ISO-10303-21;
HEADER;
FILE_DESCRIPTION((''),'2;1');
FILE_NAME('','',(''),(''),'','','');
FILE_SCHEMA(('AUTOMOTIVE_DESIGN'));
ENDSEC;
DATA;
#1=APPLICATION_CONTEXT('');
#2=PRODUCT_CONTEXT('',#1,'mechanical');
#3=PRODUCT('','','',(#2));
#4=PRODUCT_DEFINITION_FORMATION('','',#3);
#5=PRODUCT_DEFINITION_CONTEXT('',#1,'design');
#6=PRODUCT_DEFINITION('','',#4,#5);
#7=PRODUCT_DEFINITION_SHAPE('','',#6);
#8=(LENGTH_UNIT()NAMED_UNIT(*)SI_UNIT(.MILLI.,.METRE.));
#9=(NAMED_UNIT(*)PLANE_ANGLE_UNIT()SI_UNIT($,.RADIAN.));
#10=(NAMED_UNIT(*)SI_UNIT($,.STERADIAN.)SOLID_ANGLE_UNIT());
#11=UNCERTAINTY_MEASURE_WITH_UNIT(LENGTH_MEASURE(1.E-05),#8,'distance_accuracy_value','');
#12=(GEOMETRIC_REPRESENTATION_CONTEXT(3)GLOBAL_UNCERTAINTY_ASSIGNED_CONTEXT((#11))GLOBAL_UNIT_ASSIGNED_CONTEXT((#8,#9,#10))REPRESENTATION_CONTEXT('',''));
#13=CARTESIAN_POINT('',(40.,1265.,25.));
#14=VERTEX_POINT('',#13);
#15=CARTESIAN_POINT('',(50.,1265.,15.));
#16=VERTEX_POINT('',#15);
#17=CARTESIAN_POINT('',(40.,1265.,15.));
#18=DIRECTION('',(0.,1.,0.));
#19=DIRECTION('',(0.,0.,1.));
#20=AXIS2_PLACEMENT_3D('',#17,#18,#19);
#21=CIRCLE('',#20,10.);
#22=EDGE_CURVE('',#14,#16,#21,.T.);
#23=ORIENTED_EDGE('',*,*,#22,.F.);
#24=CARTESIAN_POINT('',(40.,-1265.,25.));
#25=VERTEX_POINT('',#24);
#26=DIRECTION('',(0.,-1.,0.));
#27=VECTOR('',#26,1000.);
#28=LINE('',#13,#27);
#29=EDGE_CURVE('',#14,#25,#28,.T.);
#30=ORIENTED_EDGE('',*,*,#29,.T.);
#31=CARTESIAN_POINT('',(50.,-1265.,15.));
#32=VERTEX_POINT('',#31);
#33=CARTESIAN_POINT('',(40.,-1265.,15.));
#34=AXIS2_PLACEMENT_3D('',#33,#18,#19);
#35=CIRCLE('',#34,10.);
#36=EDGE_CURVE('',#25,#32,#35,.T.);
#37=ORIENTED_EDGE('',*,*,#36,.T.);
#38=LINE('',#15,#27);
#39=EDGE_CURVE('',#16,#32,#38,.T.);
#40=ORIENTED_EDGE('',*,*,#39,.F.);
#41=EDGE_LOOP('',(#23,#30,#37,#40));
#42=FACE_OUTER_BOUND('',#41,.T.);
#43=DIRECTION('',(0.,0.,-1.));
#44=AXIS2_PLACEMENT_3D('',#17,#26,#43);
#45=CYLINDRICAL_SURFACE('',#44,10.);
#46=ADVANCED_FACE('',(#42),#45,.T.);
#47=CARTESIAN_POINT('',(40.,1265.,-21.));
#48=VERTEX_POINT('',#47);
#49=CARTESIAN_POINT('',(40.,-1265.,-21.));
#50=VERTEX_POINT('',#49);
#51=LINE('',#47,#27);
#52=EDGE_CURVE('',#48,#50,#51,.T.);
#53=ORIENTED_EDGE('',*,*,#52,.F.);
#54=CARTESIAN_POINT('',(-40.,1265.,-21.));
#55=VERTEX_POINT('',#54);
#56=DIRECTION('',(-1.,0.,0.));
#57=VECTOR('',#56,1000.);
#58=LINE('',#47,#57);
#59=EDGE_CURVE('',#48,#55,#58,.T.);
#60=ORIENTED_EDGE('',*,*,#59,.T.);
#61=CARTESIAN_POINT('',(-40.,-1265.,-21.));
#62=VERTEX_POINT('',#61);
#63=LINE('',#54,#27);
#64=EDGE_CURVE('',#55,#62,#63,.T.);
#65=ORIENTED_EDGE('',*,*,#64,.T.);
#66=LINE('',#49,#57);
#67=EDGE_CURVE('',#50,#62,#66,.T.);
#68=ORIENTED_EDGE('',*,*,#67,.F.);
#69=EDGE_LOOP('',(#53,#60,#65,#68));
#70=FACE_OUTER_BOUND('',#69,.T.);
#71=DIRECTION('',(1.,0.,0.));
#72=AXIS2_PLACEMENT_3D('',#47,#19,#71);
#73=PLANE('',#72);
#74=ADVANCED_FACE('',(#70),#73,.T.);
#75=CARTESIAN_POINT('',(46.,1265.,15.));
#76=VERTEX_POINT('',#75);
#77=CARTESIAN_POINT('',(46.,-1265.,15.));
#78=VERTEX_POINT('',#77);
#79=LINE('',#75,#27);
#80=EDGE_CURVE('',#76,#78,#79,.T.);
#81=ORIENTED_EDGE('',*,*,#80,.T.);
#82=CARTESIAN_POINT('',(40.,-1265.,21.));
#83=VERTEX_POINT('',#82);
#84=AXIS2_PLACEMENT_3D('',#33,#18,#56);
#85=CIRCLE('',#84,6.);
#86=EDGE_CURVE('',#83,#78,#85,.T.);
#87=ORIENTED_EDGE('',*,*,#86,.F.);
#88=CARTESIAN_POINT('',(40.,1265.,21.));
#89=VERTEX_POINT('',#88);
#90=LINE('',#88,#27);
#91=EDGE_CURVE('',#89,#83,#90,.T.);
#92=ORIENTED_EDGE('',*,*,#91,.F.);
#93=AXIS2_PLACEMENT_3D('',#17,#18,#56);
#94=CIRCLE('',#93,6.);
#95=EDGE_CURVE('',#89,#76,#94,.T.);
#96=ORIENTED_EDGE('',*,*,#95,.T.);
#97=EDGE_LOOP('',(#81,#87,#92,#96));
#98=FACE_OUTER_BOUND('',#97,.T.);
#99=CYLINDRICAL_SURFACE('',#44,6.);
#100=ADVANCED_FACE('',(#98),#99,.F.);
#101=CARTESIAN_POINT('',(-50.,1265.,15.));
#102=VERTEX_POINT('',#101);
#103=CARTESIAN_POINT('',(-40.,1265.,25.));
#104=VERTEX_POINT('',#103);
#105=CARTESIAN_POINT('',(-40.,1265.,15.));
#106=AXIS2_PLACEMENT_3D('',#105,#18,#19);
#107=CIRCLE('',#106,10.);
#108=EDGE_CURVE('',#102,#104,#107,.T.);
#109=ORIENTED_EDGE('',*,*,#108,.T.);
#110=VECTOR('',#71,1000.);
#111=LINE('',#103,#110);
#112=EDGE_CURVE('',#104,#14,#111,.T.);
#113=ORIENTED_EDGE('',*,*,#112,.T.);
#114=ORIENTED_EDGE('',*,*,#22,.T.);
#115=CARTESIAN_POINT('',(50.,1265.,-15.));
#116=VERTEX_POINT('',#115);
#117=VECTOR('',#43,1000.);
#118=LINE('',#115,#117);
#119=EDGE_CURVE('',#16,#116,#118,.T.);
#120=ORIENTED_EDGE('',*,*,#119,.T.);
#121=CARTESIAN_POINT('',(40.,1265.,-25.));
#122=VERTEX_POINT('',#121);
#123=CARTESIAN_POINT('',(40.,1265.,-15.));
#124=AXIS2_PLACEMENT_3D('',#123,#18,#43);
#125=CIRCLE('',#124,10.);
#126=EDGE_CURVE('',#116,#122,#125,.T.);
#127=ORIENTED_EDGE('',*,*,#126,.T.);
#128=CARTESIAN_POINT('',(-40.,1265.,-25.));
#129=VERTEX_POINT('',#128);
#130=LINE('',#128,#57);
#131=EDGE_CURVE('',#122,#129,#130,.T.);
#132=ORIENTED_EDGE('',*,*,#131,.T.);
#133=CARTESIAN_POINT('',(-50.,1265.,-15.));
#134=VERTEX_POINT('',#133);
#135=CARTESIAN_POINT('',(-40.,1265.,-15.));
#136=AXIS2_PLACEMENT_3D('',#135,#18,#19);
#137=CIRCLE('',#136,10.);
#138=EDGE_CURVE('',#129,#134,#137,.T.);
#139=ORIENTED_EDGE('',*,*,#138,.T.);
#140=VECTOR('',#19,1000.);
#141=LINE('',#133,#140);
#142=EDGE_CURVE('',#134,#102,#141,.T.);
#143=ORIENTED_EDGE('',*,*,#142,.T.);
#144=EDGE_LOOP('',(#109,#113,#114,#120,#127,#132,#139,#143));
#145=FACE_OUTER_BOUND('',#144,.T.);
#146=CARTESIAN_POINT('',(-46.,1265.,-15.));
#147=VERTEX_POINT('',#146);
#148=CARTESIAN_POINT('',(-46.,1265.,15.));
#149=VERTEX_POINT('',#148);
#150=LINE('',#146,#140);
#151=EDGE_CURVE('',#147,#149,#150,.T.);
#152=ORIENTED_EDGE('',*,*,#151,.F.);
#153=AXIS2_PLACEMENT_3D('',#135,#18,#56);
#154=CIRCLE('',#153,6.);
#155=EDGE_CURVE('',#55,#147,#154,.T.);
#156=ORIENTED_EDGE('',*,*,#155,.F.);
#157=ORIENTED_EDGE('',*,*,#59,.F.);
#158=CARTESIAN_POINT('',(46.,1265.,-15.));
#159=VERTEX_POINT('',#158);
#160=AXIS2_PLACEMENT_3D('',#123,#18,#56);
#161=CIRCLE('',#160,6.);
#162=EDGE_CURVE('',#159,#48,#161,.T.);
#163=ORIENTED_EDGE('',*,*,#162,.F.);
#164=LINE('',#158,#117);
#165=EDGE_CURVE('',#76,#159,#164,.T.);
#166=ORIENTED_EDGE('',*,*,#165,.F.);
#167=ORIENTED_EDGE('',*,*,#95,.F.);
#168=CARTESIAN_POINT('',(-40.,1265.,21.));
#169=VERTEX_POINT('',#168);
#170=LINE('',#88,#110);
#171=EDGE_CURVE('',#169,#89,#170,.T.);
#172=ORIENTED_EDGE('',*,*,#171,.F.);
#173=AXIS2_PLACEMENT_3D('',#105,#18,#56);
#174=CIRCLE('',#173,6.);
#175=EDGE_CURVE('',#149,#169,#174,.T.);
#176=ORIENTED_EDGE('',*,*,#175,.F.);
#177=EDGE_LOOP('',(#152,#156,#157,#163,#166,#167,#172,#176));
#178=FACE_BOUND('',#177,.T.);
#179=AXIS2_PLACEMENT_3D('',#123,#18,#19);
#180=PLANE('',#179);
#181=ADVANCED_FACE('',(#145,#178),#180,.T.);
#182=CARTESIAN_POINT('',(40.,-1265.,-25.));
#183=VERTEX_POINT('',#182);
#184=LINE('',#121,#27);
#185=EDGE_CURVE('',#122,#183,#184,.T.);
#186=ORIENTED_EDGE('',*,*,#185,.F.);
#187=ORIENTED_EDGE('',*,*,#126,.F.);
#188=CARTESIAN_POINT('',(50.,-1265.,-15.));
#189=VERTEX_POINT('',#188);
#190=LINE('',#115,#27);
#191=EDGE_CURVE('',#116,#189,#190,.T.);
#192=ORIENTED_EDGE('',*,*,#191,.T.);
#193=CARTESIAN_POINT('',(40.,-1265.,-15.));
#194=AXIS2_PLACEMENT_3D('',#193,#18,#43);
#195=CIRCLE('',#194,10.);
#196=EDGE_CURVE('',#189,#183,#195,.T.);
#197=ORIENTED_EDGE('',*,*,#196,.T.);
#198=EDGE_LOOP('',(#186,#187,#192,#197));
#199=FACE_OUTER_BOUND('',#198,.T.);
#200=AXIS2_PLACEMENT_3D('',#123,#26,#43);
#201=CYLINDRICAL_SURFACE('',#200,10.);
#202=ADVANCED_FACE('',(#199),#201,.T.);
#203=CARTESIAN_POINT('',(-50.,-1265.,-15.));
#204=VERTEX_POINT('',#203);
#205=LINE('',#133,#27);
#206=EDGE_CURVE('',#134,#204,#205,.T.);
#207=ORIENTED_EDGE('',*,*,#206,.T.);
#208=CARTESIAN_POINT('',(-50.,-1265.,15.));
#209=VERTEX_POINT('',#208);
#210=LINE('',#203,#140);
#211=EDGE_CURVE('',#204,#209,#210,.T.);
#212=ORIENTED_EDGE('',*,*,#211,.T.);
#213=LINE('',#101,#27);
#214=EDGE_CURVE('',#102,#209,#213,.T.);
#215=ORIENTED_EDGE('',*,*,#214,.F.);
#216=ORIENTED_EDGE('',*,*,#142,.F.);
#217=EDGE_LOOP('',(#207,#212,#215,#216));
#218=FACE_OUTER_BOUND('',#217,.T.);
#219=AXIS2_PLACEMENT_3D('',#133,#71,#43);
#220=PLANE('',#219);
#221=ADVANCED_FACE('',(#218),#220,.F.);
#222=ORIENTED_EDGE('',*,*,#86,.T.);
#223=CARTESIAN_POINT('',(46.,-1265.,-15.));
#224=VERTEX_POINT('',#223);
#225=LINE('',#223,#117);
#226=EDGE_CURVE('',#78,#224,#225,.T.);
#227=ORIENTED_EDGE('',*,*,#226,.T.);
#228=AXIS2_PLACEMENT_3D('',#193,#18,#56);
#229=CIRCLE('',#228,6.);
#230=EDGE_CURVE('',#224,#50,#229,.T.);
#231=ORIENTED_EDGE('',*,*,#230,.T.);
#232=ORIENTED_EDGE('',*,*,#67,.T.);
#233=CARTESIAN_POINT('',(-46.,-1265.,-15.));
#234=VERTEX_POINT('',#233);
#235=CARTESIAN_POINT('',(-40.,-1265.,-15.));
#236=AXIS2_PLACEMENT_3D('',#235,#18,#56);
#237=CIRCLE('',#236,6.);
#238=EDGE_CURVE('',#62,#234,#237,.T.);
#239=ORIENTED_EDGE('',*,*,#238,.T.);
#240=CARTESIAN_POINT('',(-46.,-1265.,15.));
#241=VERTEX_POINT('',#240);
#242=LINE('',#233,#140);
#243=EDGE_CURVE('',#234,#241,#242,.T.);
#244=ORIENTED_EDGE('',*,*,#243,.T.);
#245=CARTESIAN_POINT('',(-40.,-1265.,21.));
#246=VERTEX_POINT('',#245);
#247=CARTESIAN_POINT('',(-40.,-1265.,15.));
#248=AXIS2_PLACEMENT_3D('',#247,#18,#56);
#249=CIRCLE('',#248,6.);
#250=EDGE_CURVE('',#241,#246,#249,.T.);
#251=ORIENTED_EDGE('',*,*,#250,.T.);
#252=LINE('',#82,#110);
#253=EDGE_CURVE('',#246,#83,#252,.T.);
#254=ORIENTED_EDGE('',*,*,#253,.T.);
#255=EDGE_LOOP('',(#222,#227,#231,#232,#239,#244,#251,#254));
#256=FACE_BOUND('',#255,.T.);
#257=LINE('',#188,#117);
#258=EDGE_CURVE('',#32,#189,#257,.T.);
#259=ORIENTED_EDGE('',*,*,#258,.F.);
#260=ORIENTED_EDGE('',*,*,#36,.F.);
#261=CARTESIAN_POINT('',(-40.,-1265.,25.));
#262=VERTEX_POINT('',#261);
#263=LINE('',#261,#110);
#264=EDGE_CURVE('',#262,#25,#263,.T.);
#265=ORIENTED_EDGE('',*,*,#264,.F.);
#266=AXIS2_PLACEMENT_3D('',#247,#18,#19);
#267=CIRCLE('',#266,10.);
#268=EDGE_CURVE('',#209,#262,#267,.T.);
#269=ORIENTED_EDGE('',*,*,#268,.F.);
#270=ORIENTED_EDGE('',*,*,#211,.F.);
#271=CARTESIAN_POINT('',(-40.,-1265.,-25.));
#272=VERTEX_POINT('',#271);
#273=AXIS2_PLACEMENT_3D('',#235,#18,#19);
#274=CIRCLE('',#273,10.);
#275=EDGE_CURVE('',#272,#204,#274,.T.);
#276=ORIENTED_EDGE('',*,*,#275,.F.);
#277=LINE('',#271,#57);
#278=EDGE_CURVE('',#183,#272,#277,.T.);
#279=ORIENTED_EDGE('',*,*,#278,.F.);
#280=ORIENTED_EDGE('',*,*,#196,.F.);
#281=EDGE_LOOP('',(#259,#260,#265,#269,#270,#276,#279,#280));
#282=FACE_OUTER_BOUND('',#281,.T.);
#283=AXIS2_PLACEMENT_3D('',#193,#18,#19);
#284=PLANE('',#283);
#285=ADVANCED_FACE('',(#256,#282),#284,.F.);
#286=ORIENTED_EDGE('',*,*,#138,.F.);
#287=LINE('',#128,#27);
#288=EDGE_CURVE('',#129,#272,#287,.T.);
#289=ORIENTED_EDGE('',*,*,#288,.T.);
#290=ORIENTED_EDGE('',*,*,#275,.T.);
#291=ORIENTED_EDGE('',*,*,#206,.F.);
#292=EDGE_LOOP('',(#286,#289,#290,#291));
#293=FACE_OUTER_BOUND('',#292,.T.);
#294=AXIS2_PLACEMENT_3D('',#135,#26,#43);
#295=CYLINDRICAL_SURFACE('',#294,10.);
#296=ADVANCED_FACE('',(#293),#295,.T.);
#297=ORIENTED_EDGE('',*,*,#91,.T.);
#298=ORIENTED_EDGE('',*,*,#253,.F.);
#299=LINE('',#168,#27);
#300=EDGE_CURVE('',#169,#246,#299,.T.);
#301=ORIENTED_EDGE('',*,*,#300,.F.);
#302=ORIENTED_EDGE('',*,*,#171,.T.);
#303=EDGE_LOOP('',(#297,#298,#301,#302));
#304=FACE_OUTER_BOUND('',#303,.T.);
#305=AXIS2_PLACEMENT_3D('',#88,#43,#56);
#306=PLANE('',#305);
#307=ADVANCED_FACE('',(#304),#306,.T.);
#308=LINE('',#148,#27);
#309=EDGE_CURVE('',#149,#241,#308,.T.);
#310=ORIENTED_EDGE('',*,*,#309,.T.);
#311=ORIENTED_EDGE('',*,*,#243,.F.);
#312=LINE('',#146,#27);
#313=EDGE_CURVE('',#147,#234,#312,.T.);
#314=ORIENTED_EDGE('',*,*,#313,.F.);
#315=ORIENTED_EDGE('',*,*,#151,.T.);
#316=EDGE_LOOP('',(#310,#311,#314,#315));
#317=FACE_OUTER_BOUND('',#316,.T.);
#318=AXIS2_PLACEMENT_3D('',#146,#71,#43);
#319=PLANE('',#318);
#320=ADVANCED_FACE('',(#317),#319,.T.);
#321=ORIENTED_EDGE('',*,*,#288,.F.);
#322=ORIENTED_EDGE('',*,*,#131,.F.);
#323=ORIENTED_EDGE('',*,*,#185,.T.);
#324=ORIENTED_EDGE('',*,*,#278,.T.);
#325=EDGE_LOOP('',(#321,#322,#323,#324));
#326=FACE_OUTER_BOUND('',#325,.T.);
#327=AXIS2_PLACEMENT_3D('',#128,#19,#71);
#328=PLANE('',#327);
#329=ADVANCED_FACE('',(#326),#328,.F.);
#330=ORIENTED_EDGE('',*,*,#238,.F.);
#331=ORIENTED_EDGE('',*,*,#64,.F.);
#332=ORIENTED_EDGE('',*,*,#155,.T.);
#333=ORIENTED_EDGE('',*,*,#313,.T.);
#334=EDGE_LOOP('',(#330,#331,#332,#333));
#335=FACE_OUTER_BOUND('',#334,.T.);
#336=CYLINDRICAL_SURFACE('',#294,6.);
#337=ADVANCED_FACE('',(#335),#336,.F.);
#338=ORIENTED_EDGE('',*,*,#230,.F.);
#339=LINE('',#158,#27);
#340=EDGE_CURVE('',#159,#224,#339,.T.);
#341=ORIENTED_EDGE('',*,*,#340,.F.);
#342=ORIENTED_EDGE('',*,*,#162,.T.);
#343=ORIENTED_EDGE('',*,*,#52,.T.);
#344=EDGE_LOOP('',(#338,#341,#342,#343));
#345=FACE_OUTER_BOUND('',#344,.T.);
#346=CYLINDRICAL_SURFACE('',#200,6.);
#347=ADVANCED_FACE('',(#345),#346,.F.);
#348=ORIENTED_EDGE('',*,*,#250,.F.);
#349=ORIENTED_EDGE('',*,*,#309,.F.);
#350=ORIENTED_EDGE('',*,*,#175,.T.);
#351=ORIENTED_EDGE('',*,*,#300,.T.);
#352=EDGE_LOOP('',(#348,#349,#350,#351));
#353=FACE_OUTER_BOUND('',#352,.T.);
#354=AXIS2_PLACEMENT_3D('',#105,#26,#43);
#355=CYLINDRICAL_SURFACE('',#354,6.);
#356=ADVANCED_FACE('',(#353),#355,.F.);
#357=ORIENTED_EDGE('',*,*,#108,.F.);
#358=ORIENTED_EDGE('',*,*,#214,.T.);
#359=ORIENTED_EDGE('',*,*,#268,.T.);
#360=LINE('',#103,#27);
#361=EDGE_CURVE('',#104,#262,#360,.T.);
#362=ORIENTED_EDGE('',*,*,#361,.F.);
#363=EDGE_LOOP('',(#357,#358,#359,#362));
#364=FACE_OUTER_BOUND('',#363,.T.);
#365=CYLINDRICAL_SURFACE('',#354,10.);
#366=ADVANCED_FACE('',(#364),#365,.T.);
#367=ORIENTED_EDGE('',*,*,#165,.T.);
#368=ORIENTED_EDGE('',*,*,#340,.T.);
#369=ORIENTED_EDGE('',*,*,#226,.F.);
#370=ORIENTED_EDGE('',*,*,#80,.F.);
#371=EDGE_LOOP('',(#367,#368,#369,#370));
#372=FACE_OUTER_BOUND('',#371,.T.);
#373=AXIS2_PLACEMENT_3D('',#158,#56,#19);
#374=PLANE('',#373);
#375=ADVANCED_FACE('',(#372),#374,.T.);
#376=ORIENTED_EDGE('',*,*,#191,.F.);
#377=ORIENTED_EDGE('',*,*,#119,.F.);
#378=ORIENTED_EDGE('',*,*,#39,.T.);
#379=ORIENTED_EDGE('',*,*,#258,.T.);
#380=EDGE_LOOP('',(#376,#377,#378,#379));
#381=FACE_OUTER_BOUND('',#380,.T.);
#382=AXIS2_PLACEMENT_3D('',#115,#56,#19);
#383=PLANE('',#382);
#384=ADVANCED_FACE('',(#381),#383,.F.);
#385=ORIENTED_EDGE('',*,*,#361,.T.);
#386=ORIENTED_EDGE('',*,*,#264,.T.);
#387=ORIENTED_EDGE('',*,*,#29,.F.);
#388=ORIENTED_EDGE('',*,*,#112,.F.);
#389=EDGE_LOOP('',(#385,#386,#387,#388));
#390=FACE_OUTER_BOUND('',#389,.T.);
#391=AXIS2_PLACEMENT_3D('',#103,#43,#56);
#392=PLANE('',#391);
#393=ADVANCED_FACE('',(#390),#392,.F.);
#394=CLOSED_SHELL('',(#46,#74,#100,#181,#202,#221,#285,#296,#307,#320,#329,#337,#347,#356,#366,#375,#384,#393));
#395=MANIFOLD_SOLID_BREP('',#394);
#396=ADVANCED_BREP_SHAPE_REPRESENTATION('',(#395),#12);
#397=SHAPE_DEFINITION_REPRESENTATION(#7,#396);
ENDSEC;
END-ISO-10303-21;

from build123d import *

# Parameters (mm, degrees)
EXTRUDE_THIN1_DEPTH = 1265


with BuildPart() as part:
    # Sketch1 → Extrude-Thin1 (new, symmetric)
    with BuildSketch(Plane(origin=(0, 0, 0), x_dir=(1, 0, 0), z_dir=(0, 1, 0))):
        with BuildLine():
            Line((-40, 25), (40, 25))
            ThreePointArc((40, 25), (47.071067812, 22.071067812), (50, 15))
            Line((50, 15), (50, -15))
            ThreePointArc((50, -15), (47.071067812, -22.071067812), (40, -25))
            Line((40, -25), (-40, -25))
            ThreePointArc((-40, -25), (-47.071067812, -22.071067812), (-50, -15))
            Line((-50, -15), (-50, 15))
            ThreePointArc((-50, 15), (-47.071067812, 22.071067812), (-40, 25))
        make_face()
        with BuildLine():
            Line((-40, 21), (40, 21))
            ThreePointArc((40, 21), (44.242640687, 19.242640687), (46, 15))
            Line((46, 15), (46, -15))
            ThreePointArc((46, -15), (44.242640687, -19.242640687), (40, -21))
            Line((40, -21), (-40, -21))
            ThreePointArc((-40, -21), (-44.242640687, -19.242640687), (-46, -15))
            Line((-46, -15), (-46, 15))
            ThreePointArc((-46, 15), (-44.242640687, 19.242640687), (-40, 21))
        make_face(mode=Mode.SUBTRACT)
    extrude(amount=EXTRUDE_THIN1_DEPTH, both=True)


solid = part.part
